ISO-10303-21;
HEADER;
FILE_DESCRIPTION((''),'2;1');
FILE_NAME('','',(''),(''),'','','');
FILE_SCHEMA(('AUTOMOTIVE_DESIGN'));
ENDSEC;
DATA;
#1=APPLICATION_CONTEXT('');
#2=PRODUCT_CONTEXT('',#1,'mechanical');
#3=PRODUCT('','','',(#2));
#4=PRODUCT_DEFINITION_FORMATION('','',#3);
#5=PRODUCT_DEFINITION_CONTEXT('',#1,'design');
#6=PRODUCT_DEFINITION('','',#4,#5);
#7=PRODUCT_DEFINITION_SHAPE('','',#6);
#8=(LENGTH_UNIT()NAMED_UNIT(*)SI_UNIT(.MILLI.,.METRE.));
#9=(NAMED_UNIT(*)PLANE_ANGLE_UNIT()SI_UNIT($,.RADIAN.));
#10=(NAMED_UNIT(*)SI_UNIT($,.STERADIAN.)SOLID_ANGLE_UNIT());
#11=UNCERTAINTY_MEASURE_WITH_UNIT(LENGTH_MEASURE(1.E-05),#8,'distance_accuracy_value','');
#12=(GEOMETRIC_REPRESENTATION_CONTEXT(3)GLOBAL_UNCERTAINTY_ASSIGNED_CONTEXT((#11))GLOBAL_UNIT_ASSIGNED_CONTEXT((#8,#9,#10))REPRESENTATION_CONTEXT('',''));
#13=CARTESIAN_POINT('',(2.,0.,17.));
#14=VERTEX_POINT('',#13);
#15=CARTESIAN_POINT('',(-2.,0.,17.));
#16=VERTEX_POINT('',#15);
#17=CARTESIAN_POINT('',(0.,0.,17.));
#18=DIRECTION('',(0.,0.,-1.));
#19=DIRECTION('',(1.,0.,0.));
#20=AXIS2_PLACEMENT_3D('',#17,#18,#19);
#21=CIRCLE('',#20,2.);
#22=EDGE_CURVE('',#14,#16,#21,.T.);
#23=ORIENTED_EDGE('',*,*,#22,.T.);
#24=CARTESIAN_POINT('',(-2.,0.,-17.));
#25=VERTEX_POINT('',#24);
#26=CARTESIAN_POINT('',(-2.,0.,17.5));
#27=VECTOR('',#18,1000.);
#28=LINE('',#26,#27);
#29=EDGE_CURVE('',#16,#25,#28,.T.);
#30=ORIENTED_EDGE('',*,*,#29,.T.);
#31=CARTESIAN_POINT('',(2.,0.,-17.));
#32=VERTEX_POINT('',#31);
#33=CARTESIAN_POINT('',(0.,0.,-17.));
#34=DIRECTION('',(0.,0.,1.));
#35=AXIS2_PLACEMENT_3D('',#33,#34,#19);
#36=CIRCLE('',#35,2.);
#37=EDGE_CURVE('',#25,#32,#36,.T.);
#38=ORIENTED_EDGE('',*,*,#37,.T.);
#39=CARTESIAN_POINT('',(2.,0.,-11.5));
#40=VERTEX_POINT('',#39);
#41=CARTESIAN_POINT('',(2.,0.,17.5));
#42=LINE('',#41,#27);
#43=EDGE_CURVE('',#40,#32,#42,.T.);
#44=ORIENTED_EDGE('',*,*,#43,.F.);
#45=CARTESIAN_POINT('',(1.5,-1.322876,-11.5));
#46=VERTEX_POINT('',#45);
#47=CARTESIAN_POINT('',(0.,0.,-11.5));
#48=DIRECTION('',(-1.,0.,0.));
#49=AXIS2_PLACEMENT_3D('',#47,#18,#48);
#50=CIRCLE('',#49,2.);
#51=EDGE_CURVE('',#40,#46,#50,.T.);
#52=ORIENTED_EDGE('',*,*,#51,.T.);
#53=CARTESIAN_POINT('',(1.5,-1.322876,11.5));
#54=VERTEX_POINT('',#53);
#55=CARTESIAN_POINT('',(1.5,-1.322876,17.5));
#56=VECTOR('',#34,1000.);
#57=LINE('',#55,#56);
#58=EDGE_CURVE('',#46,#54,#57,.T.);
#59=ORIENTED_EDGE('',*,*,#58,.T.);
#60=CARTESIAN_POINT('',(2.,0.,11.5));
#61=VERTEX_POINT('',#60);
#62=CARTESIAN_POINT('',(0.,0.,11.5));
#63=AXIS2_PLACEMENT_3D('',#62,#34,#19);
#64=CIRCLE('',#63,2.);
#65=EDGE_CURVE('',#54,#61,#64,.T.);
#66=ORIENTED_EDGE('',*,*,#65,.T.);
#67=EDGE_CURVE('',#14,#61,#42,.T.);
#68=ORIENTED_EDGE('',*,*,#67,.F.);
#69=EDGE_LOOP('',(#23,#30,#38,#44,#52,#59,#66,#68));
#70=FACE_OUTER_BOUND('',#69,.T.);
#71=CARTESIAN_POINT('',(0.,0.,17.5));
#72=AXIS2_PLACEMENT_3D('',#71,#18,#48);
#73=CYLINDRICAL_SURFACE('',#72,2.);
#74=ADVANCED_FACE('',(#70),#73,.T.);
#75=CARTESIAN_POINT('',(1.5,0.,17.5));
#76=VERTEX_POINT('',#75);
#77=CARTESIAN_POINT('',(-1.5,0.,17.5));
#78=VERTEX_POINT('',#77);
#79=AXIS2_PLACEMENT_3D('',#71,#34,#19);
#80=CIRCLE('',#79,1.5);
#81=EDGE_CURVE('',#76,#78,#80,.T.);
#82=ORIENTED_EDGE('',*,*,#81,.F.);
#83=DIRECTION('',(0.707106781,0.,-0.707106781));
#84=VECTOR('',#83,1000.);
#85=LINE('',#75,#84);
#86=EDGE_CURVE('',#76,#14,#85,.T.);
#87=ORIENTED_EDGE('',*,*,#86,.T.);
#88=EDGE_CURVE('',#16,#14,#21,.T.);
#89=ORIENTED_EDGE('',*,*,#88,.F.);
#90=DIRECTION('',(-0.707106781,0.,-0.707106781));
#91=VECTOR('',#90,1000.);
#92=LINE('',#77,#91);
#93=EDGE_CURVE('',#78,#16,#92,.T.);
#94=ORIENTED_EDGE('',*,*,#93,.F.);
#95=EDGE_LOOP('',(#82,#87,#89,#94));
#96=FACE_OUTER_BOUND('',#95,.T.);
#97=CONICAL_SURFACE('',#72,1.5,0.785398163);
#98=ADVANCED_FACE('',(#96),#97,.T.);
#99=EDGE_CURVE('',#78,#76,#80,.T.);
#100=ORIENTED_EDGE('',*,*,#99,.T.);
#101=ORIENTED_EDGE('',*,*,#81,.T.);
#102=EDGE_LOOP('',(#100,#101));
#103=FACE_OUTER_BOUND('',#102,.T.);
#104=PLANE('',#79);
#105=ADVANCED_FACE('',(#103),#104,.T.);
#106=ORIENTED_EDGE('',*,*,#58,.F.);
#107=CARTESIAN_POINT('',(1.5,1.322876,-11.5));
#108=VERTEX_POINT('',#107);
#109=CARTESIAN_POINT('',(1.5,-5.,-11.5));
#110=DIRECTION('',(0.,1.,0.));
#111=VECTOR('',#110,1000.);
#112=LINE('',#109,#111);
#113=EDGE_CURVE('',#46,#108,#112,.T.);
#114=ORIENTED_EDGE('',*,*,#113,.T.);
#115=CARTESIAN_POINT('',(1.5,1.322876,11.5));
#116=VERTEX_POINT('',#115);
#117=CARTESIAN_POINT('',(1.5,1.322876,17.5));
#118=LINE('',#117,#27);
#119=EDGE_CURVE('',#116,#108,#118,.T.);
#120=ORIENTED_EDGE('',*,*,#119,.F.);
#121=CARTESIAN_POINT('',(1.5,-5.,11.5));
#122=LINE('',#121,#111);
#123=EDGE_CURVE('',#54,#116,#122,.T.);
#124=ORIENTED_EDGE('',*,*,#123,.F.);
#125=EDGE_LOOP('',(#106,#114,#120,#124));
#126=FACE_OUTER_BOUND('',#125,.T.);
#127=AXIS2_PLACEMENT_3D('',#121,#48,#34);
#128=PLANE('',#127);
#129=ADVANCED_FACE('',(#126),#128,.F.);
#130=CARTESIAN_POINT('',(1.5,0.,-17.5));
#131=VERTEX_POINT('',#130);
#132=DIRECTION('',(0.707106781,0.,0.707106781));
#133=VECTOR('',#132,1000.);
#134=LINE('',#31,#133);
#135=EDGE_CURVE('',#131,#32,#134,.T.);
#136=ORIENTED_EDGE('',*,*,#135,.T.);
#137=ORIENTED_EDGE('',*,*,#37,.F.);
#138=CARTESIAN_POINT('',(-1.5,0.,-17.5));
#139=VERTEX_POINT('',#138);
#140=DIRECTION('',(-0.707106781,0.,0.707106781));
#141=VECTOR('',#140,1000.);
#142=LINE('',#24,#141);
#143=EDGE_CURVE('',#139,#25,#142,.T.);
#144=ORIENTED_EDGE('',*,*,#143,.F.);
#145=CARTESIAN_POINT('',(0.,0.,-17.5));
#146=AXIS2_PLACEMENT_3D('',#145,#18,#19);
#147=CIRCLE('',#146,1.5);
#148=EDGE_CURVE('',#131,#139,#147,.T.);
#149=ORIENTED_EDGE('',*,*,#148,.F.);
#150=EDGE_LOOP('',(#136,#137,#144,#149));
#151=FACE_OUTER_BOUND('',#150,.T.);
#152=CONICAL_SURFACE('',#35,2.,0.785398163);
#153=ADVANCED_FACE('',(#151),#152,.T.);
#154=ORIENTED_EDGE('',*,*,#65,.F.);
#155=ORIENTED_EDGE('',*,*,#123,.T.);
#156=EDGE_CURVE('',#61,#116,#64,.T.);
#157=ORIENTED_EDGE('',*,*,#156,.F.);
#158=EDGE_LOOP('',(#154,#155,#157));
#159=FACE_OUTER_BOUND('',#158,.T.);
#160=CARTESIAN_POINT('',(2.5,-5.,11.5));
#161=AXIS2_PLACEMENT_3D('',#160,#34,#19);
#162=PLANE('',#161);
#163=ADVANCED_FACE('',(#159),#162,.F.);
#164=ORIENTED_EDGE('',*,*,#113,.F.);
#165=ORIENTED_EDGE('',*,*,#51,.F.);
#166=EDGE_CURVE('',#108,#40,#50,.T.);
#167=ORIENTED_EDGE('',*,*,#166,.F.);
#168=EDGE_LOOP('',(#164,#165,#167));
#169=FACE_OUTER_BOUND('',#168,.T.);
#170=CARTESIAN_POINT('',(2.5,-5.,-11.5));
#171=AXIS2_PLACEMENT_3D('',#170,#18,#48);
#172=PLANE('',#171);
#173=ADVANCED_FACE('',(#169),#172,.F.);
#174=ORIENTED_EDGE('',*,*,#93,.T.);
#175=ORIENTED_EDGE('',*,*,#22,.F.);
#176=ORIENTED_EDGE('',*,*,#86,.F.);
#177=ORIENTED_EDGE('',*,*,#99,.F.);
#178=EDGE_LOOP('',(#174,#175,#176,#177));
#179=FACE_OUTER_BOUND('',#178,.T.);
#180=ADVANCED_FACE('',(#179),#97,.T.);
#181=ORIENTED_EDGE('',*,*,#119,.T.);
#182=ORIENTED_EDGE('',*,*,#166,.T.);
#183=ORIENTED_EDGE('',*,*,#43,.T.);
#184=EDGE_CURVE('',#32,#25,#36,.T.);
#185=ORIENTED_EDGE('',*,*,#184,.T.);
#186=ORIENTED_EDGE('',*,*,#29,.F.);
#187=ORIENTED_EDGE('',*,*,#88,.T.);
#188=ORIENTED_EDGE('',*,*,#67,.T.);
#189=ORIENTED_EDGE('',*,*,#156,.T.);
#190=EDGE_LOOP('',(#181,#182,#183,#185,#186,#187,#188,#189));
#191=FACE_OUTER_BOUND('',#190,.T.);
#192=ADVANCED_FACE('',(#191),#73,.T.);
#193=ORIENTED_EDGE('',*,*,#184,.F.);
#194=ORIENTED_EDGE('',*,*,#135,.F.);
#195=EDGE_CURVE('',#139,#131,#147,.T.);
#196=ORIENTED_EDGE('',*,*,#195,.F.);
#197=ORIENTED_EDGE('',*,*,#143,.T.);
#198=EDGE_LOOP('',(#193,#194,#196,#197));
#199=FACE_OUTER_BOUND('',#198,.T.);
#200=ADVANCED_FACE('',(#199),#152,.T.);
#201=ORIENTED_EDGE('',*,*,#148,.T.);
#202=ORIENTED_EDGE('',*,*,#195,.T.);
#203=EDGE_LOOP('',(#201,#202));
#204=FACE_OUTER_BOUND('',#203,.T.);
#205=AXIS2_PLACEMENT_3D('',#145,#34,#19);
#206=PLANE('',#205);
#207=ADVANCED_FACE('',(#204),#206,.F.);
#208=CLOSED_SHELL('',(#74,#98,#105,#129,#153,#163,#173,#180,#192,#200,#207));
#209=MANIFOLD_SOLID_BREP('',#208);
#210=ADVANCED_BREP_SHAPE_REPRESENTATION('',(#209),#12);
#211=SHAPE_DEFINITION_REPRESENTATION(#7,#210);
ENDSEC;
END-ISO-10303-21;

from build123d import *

# Parameters (mm, degrees)
SKETCH1_R           = 2
BOSS_EXTRUDE1_DEPTH = 17.5
CHAMFER1_SIZE       = 0.5
SKETCH2_W           = 1
SKETCH2_H           = 23
CUT_EXTRUDE1_DEPTH  = 5


with BuildPart() as part:
    # Sketch1 → Boss-Extrude1 (new, symmetric)
    with BuildSketch(Plane.XY):
        Circle(SKETCH1_R)
    extrude(amount=BOSS_EXTRUDE1_DEPTH, both=True)

    # Chamfer1
    chamfer1_edges = [part.edges().sort_by_distance(p)[0] for p in [
        (-2, 0, -17.5),
        (-2, 0, 17.5),
    ]]
    chamfer(chamfer1_edges, length=CHAMFER1_SIZE)

    # Sketch2 → Cut-Extrude1 (cut, symmetric)
    with BuildSketch(Plane(origin=(0, 0, 0), x_dir=(1, 0, 0), z_dir=(0, 1, 0))):
        with Locations((2, 0)):
            Rectangle(SKETCH2_W, SKETCH2_H)
    extrude(amount=CUT_EXTRUDE1_DEPTH, both=True, mode=Mode.SUBTRACT)


solid = part.part
